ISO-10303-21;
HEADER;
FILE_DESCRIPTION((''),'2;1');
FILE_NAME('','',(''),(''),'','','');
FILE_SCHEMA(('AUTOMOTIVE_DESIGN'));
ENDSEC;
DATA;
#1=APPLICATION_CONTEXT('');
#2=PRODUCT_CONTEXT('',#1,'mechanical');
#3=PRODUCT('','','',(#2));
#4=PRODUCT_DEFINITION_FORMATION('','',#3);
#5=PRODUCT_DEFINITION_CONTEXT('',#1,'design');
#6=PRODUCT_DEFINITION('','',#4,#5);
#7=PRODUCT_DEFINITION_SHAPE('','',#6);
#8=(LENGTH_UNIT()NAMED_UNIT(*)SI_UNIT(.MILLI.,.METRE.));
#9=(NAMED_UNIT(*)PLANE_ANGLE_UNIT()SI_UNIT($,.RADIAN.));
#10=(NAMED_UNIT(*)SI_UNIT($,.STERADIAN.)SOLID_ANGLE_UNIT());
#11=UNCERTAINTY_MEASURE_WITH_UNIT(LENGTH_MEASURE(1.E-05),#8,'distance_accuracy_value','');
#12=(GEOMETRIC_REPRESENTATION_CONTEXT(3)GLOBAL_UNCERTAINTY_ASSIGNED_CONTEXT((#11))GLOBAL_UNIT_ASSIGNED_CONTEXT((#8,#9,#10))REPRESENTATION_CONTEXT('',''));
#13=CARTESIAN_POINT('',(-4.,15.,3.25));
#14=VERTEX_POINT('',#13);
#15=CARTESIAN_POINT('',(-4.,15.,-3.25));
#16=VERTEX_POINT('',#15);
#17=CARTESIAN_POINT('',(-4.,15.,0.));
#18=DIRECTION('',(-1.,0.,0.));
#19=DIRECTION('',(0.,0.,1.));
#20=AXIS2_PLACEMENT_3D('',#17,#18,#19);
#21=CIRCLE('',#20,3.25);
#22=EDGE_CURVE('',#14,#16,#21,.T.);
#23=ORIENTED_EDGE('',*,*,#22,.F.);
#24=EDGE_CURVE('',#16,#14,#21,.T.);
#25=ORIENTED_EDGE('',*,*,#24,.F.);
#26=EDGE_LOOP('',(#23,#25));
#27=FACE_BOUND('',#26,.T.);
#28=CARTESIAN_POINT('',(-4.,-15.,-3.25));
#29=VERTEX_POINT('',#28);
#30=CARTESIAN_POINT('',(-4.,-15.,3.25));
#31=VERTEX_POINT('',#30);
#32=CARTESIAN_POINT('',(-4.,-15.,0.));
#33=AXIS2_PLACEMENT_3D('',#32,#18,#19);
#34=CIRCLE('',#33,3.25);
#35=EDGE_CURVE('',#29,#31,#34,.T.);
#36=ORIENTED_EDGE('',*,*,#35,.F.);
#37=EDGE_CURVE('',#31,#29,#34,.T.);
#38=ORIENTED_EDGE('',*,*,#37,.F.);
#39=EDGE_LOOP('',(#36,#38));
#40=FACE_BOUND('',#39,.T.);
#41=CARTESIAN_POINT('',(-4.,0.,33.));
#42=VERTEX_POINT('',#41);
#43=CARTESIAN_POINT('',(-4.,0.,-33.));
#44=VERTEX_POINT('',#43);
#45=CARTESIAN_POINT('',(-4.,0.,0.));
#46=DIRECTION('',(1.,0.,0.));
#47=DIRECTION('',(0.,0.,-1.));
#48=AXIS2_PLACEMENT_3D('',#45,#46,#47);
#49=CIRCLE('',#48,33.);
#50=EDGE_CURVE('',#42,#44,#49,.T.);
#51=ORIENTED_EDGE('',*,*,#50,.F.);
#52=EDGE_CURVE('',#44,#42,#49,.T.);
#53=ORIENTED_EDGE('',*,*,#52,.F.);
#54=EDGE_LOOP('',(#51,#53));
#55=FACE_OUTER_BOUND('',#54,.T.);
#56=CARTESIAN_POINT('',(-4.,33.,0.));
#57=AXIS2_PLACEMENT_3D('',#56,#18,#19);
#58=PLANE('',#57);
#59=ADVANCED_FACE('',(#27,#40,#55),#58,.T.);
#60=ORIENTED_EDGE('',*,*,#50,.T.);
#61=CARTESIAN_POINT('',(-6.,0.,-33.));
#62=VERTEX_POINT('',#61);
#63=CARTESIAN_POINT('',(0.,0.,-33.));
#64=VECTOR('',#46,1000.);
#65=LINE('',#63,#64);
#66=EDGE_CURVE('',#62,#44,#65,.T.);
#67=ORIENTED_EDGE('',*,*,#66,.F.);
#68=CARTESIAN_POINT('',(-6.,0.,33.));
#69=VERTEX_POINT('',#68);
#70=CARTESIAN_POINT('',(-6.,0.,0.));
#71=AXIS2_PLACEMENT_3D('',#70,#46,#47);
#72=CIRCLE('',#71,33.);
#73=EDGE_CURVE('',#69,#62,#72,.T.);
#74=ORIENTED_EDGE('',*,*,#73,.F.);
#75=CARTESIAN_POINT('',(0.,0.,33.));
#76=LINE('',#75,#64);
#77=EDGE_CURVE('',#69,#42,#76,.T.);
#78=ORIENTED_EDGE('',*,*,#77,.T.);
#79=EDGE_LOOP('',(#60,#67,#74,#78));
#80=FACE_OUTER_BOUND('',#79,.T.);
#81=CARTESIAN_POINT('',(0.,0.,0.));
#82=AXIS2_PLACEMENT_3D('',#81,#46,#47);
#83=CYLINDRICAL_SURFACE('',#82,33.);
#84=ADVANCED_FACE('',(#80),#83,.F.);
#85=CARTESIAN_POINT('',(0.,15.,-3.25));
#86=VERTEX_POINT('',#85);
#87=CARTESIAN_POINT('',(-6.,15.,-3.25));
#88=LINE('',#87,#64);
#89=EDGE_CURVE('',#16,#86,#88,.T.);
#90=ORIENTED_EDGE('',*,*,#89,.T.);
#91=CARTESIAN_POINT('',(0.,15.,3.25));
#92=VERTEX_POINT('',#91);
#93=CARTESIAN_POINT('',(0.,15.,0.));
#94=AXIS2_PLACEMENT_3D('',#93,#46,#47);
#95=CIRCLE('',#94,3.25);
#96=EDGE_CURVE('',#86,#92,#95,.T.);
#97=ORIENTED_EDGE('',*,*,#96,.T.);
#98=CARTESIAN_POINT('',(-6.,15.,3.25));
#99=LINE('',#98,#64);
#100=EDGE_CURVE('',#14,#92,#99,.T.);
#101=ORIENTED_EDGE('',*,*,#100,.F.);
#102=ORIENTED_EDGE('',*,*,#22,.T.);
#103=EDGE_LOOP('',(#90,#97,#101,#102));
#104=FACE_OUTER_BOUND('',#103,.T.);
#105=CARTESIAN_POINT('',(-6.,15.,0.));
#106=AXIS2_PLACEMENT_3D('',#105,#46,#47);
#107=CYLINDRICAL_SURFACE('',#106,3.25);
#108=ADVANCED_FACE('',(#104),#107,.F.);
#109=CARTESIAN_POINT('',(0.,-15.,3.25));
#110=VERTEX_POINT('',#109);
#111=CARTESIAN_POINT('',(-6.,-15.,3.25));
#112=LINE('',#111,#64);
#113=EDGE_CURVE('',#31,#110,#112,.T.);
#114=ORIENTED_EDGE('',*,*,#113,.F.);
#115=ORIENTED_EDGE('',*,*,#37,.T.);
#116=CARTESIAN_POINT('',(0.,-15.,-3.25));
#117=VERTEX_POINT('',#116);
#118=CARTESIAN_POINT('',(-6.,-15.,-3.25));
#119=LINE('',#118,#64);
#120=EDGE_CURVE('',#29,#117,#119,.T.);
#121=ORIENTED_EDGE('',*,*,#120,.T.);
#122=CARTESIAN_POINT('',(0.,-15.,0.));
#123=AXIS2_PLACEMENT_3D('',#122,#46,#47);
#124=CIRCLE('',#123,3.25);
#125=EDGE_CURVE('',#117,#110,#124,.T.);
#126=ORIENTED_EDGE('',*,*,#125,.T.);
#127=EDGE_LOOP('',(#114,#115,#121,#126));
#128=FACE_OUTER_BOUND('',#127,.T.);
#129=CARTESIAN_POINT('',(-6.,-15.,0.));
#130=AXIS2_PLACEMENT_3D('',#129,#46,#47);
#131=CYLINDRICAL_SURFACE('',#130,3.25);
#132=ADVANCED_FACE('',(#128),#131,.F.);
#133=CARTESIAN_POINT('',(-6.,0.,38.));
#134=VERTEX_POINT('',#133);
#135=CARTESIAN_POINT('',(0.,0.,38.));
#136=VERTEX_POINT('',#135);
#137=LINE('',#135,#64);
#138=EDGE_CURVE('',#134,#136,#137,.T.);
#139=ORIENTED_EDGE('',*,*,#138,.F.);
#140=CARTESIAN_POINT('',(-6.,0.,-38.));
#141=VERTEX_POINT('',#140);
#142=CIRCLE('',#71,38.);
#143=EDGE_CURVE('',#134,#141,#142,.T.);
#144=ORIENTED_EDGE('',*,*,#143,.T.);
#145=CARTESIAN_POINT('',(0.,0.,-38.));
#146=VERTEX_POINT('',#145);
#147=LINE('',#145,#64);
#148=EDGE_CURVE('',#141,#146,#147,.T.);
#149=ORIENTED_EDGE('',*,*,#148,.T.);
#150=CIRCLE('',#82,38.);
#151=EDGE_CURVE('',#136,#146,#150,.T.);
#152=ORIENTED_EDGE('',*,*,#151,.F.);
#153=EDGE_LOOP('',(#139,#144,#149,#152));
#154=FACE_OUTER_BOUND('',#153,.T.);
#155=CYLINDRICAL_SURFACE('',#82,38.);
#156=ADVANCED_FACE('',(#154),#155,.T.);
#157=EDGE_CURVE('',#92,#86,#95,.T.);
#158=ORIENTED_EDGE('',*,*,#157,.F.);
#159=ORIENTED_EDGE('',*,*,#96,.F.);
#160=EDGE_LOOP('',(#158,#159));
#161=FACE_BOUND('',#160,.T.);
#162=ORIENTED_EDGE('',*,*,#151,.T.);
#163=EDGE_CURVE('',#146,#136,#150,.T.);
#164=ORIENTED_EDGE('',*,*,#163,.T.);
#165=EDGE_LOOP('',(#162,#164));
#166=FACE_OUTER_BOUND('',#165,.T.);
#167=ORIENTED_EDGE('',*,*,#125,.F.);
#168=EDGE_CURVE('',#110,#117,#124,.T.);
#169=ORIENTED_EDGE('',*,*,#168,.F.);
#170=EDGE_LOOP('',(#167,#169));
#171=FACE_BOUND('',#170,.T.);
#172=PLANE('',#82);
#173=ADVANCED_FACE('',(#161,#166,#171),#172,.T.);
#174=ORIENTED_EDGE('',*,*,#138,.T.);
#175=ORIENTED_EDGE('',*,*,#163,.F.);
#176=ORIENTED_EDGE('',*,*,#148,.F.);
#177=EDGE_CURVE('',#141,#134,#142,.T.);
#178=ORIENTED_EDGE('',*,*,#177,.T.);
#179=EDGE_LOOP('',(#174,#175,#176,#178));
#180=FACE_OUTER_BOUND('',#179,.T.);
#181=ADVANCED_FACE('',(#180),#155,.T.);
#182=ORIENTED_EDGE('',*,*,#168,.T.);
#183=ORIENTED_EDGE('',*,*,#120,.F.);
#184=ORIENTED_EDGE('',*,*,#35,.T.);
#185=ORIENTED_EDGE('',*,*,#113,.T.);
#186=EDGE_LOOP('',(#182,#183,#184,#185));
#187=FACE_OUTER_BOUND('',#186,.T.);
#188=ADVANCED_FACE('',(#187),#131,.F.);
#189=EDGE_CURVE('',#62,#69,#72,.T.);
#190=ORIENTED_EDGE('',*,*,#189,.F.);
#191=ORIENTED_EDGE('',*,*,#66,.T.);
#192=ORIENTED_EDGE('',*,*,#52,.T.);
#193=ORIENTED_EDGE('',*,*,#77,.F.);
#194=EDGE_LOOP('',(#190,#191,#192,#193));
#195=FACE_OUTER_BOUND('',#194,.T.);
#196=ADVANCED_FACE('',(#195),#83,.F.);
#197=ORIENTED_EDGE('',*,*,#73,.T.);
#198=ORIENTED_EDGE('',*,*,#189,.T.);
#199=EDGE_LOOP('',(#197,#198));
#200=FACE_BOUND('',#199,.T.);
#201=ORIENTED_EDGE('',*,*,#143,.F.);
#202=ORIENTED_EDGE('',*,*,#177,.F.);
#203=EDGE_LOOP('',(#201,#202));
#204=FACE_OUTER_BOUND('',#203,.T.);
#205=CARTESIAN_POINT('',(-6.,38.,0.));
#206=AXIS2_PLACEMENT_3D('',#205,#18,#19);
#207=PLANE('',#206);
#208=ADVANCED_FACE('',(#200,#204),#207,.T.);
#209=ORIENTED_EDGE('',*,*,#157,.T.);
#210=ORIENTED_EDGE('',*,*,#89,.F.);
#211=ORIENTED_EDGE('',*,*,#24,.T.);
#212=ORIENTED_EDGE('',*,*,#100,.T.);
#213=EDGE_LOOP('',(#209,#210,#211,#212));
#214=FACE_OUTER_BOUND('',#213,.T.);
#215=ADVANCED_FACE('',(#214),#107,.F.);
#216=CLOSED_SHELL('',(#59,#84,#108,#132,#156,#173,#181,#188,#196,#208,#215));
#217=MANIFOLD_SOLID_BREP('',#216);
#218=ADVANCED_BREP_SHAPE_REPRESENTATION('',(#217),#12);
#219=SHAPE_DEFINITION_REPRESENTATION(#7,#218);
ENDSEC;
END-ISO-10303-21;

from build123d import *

# Parameters (mm, degrees)
SKETCH2_R          = 3.25
CUT_EXTRUDE1_DEPTH = 55.074023338


with BuildPart() as part:
    # Sketch1 → Revolve1 (revolve)
    with BuildSketch(Plane.XY, mode=Mode.PRIVATE) as revolve1_sk:
        Polygon((0, 0), (0, 38), (-6, 38), (-6, 33), (-4, 33), (-4, 0), align=None)
    revolve(revolve1_sk.sketch.rotate(Axis((0, 0, 0), (-1, 0, 0)), 90), axis=Axis((0, 0, 0), (-1, 0, 0)))

    # Sketch2 → Cut-Extrude1 (cut, through all)
    with BuildSketch(Plane(origin=(0, 0, 0), x_dir=(0, 0, -1), z_dir=(1, 0, 0))):
        with Locations((0, 15)):
            Circle(SKETCH2_R)
        with Locations((0, -15)):
            Circle(SKETCH2_R)
    extrude(amount=-CUT_EXTRUDE1_DEPTH, mode=Mode.SUBTRACT)


solid = part.part
